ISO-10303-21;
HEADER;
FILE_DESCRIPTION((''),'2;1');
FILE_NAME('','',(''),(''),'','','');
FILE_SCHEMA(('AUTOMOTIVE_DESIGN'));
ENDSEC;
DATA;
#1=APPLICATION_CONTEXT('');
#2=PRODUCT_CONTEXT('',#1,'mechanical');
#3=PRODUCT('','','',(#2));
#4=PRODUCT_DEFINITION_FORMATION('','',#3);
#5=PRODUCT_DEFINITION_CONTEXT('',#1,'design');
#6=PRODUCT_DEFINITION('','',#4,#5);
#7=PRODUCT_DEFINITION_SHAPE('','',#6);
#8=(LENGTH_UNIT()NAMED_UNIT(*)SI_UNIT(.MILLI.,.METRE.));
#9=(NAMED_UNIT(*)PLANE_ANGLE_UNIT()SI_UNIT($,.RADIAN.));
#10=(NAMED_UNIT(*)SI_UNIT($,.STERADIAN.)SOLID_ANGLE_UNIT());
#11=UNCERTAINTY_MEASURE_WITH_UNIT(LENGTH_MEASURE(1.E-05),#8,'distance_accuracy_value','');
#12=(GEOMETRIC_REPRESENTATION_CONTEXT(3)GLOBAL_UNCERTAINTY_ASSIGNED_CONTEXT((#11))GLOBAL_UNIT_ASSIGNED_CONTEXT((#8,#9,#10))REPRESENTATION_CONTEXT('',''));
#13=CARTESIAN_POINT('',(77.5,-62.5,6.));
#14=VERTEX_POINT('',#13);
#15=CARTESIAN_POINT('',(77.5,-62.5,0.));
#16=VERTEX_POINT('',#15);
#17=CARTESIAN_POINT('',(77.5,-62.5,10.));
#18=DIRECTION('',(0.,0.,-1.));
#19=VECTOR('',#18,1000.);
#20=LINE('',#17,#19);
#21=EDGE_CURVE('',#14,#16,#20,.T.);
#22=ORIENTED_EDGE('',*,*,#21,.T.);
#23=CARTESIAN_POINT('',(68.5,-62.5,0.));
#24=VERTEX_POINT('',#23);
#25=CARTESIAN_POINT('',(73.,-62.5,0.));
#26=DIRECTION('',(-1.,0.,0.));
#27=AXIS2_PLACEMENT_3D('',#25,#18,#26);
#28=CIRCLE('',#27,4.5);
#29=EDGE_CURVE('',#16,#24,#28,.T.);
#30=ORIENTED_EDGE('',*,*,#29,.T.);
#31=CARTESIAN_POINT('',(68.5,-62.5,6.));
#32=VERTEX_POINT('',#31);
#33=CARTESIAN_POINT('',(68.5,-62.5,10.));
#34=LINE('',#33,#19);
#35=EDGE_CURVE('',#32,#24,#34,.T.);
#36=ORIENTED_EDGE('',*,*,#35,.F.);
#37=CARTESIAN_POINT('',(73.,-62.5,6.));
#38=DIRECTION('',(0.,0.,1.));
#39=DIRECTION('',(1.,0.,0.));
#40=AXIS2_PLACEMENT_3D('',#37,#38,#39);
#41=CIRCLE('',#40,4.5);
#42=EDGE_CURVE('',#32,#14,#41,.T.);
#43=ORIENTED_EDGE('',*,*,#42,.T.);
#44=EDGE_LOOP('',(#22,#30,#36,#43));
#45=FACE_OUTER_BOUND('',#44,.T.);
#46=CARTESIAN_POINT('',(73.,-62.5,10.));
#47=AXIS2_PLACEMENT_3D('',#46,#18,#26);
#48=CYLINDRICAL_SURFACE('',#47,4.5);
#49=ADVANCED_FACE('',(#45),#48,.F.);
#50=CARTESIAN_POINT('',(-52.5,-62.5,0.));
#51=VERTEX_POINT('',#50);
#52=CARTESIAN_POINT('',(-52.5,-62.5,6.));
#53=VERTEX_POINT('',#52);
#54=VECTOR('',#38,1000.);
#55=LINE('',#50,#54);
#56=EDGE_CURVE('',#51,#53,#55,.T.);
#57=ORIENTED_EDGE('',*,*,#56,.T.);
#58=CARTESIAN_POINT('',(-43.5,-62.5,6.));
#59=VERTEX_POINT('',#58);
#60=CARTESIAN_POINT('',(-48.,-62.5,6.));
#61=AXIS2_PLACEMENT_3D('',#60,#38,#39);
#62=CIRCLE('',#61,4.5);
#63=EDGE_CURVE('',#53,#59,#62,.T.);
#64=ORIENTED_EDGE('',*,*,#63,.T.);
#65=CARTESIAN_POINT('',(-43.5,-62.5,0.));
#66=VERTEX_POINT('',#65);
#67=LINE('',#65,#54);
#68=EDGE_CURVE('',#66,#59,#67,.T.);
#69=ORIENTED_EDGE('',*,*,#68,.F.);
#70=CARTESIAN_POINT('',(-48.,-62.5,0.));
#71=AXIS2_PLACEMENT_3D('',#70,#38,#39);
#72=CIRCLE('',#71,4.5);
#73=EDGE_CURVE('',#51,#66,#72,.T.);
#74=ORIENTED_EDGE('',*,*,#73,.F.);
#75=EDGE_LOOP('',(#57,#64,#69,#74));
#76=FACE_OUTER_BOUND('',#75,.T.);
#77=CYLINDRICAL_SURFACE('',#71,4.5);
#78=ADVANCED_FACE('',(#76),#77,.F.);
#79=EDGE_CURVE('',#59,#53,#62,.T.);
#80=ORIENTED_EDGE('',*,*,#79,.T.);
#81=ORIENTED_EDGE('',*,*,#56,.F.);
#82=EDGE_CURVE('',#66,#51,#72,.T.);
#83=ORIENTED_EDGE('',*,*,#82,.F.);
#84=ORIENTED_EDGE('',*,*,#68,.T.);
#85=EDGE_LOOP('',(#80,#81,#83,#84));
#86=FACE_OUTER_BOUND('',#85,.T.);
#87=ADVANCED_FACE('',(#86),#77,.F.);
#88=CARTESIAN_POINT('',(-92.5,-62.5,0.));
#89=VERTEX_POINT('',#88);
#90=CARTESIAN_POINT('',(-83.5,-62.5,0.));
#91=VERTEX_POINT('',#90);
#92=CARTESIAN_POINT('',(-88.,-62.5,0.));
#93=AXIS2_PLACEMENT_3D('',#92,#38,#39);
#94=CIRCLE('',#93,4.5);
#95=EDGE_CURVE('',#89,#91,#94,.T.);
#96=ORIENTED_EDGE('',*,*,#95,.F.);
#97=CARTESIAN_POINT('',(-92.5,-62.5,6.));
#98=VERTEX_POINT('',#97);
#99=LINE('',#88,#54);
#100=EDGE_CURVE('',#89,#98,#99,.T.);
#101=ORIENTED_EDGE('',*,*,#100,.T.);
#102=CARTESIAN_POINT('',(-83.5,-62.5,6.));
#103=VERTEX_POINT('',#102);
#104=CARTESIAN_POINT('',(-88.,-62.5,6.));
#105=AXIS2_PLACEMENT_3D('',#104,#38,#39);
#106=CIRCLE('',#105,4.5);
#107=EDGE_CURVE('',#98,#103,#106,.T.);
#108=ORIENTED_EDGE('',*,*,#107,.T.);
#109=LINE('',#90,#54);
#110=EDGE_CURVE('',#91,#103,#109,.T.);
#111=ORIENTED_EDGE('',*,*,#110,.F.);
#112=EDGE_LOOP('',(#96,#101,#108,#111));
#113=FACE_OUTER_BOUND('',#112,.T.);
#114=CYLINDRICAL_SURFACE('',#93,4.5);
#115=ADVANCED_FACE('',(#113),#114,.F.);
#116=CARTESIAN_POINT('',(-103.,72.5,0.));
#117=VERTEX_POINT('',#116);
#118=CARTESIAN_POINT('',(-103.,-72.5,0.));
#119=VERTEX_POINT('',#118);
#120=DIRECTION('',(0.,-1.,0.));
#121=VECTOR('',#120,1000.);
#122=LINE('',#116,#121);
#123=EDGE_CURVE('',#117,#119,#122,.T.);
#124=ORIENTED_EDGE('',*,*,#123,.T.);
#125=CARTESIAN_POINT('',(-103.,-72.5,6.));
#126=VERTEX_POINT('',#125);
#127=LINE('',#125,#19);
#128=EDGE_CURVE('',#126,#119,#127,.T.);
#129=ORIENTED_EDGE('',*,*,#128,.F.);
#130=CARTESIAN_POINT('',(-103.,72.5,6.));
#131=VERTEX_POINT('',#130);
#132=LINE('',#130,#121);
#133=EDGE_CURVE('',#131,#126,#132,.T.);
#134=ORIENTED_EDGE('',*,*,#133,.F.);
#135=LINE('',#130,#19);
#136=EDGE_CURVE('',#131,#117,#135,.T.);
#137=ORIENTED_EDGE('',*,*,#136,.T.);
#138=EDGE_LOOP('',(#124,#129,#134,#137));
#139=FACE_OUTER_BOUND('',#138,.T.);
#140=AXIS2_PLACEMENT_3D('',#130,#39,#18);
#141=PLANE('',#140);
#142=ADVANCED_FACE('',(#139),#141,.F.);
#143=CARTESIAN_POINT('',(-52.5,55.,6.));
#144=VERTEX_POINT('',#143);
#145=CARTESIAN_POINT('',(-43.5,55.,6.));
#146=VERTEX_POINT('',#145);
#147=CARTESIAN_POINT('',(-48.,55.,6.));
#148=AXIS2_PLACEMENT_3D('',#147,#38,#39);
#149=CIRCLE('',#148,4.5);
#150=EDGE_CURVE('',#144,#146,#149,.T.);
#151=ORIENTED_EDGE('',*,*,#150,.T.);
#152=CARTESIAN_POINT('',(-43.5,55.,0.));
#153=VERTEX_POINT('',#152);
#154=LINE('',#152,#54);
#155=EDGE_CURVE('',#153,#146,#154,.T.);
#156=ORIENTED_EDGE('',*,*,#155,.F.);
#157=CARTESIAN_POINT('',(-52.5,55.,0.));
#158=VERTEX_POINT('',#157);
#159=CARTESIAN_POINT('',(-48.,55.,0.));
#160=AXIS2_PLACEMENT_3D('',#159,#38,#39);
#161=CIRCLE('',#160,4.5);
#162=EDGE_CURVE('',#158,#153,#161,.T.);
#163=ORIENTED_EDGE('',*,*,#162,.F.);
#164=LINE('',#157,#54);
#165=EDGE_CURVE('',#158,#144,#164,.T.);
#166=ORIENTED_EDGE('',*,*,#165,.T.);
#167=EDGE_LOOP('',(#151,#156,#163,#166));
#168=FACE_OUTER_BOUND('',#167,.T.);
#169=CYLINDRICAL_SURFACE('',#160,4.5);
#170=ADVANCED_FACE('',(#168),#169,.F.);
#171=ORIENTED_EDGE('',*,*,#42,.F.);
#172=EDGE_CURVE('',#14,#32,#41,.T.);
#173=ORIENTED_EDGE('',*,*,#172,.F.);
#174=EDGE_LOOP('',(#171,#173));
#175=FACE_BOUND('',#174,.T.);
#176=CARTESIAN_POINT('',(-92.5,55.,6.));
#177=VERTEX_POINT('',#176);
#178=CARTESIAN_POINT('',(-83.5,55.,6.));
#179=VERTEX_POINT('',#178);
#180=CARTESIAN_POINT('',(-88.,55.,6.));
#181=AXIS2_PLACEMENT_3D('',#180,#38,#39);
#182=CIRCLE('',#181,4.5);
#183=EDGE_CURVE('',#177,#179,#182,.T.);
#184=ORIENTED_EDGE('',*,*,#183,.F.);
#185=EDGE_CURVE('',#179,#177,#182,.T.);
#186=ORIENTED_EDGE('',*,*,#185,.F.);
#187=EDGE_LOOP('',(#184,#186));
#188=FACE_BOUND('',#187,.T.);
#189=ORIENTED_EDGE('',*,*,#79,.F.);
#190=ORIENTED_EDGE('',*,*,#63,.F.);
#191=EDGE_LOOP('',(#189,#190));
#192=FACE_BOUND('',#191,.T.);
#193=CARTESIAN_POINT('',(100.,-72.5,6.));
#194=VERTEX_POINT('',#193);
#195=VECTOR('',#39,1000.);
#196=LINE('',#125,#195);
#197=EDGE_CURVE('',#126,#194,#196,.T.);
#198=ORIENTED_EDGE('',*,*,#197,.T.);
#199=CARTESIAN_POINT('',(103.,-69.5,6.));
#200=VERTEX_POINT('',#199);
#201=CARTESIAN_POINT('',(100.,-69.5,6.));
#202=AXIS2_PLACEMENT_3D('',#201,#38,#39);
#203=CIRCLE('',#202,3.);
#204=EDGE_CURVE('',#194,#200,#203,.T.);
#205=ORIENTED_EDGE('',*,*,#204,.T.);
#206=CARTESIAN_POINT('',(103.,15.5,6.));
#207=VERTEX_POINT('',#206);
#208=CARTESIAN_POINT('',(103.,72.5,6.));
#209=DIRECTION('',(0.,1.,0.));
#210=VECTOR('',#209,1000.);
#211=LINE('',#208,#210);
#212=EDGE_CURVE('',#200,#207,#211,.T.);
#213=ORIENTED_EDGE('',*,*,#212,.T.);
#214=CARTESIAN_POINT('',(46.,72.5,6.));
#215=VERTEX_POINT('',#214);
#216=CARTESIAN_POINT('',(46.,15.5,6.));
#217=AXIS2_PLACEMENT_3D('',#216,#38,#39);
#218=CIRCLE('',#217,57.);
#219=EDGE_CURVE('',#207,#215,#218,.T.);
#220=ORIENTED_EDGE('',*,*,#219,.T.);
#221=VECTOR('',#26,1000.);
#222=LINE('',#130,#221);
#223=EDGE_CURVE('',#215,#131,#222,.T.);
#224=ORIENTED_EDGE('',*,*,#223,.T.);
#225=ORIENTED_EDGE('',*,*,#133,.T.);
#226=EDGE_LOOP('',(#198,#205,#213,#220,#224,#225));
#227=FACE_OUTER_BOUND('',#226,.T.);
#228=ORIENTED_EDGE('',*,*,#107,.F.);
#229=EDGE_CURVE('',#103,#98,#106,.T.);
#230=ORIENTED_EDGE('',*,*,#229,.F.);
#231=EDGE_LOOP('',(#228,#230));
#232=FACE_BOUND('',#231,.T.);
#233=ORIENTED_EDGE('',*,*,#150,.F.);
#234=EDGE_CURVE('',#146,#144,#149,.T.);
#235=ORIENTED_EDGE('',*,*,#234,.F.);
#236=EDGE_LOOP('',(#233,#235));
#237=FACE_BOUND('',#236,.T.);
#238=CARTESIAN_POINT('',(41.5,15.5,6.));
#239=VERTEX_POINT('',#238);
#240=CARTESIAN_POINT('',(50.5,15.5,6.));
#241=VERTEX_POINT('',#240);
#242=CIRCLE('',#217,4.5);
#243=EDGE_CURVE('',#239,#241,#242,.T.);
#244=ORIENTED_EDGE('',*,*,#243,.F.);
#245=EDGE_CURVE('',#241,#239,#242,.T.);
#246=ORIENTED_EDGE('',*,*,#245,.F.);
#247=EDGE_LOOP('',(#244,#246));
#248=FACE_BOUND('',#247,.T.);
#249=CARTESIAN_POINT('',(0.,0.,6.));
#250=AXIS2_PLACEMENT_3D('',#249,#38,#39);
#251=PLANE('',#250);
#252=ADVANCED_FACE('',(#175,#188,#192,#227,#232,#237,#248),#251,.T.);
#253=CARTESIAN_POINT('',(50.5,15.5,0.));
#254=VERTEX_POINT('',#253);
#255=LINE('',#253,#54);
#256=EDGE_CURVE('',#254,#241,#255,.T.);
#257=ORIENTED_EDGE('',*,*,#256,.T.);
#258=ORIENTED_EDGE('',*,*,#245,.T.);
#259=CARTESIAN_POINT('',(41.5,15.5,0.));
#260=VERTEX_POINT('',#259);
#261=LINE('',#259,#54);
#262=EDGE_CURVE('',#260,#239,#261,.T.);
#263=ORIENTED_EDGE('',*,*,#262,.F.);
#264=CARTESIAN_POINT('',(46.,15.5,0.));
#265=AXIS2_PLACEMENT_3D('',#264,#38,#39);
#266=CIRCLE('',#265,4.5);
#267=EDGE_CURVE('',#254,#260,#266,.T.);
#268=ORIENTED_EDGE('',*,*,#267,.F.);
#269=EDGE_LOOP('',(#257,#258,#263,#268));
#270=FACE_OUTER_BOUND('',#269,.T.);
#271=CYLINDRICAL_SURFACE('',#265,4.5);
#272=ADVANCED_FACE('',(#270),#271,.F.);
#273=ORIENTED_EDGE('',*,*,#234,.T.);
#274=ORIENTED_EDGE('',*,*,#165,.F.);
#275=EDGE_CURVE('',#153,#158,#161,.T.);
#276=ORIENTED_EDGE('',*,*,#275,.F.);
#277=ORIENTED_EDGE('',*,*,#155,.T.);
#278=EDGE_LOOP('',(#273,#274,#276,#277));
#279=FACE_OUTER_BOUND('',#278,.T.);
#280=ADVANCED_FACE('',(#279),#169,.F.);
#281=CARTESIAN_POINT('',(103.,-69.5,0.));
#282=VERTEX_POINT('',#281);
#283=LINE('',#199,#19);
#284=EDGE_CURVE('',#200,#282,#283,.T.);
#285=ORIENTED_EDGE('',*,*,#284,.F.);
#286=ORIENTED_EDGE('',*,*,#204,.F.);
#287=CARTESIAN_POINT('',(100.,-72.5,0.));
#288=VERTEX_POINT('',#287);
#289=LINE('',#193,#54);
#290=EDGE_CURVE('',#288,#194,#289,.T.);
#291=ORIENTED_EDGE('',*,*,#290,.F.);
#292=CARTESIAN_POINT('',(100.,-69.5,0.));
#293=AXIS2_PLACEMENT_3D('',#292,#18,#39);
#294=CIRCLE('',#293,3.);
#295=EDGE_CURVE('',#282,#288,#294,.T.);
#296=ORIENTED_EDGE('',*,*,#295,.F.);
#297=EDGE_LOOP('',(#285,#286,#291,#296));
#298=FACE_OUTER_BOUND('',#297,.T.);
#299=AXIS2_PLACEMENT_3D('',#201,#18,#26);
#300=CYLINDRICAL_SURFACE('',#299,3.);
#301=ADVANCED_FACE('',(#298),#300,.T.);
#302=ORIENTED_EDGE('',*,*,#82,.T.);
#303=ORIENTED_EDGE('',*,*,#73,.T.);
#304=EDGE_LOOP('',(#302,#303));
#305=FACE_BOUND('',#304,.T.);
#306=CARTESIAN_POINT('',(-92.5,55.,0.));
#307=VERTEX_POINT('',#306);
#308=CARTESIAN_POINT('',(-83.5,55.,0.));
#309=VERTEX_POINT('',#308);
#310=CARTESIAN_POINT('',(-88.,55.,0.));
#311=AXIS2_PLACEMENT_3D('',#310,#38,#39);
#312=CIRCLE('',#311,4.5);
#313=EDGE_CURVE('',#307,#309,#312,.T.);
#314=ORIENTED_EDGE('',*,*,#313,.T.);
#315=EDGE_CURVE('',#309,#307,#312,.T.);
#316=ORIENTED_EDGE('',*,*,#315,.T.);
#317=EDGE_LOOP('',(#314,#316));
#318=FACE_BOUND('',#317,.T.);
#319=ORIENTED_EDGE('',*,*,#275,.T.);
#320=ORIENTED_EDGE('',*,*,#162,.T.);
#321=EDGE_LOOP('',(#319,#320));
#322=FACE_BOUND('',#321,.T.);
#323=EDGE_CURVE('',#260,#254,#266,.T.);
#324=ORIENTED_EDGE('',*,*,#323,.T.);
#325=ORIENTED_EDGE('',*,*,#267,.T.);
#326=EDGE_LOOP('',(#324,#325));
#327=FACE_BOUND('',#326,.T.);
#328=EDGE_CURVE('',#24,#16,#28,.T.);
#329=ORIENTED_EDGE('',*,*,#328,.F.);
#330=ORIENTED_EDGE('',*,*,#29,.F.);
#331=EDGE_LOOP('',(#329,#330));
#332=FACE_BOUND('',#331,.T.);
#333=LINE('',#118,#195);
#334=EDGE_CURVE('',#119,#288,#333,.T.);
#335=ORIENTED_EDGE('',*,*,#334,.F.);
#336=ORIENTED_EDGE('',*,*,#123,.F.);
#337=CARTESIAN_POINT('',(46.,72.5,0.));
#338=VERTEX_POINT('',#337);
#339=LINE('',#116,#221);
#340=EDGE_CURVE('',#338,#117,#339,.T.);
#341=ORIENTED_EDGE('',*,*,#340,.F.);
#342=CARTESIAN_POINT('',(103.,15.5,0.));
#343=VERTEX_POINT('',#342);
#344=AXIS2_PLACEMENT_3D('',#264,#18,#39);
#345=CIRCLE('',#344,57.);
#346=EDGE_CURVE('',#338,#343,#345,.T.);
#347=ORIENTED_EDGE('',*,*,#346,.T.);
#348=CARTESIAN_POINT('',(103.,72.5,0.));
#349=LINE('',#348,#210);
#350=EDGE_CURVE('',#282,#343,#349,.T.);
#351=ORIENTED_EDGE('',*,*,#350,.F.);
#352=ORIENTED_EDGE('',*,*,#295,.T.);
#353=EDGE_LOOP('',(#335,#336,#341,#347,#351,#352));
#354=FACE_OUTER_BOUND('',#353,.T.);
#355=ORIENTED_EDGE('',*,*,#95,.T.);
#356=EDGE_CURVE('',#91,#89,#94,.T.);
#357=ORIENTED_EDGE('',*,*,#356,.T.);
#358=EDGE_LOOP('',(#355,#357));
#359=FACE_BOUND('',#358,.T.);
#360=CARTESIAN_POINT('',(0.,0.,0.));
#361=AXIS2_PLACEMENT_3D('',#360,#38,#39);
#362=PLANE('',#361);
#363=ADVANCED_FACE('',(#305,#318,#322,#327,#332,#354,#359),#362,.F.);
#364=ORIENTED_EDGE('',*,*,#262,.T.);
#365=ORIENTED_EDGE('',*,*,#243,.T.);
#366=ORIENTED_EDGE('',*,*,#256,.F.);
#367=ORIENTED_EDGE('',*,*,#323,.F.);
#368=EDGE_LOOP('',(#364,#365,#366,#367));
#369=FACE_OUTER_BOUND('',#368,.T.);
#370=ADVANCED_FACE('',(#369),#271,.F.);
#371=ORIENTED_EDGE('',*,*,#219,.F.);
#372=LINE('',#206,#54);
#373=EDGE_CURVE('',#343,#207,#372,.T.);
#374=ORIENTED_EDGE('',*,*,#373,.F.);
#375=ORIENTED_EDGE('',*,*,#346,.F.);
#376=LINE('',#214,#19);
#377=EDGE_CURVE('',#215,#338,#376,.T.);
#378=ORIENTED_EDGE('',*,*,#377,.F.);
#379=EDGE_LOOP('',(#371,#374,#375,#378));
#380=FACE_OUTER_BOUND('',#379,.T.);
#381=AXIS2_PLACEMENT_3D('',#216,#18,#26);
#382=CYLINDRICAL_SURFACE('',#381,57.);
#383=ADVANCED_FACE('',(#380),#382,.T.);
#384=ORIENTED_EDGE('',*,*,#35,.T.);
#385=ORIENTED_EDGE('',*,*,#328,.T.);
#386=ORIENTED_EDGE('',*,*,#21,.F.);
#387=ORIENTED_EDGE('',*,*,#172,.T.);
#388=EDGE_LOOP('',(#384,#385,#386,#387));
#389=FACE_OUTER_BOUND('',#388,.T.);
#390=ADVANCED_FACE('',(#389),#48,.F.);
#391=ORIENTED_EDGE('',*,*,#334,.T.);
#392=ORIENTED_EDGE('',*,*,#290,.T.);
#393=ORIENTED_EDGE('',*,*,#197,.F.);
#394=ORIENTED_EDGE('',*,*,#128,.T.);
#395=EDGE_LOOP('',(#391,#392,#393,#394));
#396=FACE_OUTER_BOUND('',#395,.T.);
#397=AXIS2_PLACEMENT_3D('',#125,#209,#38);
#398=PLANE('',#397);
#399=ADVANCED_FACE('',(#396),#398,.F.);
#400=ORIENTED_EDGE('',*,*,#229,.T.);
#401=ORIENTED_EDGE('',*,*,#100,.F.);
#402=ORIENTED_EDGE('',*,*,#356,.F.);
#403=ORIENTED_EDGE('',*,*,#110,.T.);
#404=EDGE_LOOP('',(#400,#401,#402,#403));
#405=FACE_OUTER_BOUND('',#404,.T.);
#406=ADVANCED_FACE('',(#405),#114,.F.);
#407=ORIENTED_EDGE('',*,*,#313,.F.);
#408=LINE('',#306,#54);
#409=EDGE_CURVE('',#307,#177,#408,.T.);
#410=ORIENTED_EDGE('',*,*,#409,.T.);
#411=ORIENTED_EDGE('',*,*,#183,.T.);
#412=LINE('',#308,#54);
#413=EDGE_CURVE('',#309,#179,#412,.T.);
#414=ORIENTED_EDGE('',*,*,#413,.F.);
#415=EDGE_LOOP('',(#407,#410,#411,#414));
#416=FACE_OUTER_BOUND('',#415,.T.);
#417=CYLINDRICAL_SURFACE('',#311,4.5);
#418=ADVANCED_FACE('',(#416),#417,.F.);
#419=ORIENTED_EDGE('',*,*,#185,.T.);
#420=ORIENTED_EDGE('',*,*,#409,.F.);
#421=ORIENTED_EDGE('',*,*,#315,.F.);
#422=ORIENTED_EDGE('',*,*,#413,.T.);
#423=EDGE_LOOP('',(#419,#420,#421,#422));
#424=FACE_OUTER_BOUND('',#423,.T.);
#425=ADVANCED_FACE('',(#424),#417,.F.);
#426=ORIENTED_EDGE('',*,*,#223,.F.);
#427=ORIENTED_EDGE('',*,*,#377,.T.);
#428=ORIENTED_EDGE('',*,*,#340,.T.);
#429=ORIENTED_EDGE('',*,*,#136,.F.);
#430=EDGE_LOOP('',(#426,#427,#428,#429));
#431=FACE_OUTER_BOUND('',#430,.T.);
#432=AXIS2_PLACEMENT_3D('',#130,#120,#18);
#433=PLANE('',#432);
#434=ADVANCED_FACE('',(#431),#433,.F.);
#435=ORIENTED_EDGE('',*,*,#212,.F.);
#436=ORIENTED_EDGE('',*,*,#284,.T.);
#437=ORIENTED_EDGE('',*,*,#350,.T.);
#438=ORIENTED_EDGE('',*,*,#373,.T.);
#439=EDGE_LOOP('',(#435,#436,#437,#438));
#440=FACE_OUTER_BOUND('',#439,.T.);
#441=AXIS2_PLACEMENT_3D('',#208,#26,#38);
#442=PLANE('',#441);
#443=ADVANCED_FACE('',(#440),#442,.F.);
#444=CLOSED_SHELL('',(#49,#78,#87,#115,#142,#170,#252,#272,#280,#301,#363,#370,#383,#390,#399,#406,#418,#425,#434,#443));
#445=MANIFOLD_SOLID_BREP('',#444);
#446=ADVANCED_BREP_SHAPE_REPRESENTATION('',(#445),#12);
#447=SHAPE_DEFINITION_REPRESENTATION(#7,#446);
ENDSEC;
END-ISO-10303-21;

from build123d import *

# Parameters (mm, degrees)
SKETCH_1_W          = 206
SKETCH_1_H          = 145
EXTRUDE_1_DEPTH     = 6
SKETCH_3_R          = 4.5
CUT_EXTRUDE_2_DEPTH = 127.100158604
SKETCH_4_R          = 4.5
CUT_EXTRUDE_3_DEPTH = 127.100158604
FILLET_4_R          = 57
SKETCH_10_R         = 4.5
CUT_EXTRUDE_6_DEPTH = 10
FILLET_6_R          = 3


with BuildPart() as part:
    # 草图1 → 凸台-拉伸1 (new body)
    with BuildSketch(Plane.XY):
        Rectangle(SKETCH_1_W, SKETCH_1_H)
    extrude(amount=EXTRUDE_1_DEPTH)

    # 草图3 → 切除-拉伸2 (cut, through all)
    with BuildSketch(Plane.XY.offset(6)):
        with Locations((-88, 55)):
            Circle(SKETCH_3_R)
        with Locations((-48, 55)):
            Circle(SKETCH_3_R)
        with Locations((-88, -62.5)):
            Circle(SKETCH_3_R)
        with Locations((-48, -62.5)):
            Circle(SKETCH_3_R)
    extrude(amount=-CUT_EXTRUDE_2_DEPTH, mode=Mode.SUBTRACT)

    # 草图4 → 切除-拉伸3 (cut, through all)
    with BuildSketch(Plane.XY.offset(6)):
        with Locations((46, 15.5)):
            Circle(SKETCH_4_R)
    extrude(amount=-CUT_EXTRUDE_3_DEPTH, mode=Mode.SUBTRACT)

    # 圆角4
    fillet_4_edges = [part.edges().sort_by_distance(p)[0] for p in [
        (103, 72.5, 3),
    ]]
    fillet(fillet_4_edges, radius=FILLET_4_R)

    # 草图10 → 切除-拉伸6 (cut)
    with BuildSketch(Plane(origin=(0, 0, 0), x_dir=(-1, 0, 0), z_dir=(0, 0, -1))):
        with Locations((-73, -62.5)):
            Circle(SKETCH_10_R)
    extrude(amount=-CUT_EXTRUDE_6_DEPTH, mode=Mode.SUBTRACT)

    # 圆角6
    fillet_6_edges = [part.edges().sort_by_distance(p)[0] for p in [
        (103, -72.5, 3),
    ]]
    fillet(fillet_6_edges, radius=FILLET_6_R)


solid = part.part
